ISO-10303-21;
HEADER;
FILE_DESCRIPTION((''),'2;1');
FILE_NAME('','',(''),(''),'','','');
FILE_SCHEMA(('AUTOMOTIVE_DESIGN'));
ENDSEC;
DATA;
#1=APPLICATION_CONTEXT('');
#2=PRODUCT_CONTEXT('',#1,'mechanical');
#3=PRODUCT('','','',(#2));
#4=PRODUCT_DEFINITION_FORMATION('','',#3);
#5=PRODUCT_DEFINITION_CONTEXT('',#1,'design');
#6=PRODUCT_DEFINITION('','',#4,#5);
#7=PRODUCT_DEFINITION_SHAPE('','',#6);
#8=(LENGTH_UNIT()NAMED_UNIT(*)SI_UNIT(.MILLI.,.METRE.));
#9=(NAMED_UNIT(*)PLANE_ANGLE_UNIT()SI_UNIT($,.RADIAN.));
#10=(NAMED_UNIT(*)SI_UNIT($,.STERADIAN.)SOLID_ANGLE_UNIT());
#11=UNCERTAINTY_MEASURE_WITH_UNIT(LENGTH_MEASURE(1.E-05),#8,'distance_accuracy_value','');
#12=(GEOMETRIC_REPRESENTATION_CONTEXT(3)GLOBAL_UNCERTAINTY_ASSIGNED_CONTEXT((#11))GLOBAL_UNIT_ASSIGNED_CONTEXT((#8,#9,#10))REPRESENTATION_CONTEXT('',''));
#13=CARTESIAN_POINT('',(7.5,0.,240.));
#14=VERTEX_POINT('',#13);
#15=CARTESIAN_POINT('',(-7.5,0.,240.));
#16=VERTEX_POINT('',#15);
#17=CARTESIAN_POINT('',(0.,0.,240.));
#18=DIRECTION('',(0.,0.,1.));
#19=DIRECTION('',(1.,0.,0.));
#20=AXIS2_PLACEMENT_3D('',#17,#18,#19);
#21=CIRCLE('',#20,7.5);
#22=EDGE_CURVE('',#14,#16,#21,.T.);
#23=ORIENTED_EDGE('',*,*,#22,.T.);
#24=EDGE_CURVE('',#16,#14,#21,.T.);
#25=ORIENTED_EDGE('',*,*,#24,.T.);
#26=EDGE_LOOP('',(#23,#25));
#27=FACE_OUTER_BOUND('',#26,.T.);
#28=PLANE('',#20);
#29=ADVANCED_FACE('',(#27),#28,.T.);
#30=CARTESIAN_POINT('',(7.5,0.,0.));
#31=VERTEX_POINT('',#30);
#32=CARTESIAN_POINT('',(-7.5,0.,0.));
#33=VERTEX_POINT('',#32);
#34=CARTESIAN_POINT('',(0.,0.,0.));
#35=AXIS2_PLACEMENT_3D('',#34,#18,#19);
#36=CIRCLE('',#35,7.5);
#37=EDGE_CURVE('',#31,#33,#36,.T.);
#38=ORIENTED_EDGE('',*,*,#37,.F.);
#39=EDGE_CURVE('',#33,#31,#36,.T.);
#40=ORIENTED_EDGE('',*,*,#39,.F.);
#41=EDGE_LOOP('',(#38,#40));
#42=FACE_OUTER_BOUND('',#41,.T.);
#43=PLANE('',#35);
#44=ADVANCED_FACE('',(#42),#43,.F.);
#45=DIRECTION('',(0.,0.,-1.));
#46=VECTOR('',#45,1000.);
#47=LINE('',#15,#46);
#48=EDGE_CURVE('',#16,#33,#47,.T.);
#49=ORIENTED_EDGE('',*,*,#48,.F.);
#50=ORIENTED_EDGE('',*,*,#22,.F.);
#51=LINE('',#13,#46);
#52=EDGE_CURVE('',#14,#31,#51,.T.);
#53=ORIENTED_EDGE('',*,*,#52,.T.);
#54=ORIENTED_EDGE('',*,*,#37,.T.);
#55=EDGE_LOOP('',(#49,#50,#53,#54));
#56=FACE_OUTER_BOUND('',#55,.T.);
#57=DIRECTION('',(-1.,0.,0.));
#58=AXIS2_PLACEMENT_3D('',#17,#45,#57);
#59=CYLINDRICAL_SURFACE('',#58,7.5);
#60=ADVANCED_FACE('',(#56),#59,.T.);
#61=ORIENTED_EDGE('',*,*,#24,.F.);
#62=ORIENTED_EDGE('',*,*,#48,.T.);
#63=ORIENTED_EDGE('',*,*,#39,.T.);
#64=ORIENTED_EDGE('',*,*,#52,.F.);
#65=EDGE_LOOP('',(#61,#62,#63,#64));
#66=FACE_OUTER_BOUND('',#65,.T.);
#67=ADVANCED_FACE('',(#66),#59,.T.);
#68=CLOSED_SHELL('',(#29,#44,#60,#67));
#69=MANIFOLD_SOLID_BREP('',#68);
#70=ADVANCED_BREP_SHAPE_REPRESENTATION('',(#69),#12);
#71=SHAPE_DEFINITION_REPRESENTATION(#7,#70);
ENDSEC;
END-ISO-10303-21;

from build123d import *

# Parameters (mm, degrees)
SKETCH_1_R      = 7.5
EXTRUDE_1_DEPTH = 240


with BuildPart() as part:
    # 草图1 → 凸台-拉伸1 (new body)
    with BuildSketch(Plane.XY):
        Circle(SKETCH_1_R)
    extrude(amount=EXTRUDE_1_DEPTH)


solid = part.part
